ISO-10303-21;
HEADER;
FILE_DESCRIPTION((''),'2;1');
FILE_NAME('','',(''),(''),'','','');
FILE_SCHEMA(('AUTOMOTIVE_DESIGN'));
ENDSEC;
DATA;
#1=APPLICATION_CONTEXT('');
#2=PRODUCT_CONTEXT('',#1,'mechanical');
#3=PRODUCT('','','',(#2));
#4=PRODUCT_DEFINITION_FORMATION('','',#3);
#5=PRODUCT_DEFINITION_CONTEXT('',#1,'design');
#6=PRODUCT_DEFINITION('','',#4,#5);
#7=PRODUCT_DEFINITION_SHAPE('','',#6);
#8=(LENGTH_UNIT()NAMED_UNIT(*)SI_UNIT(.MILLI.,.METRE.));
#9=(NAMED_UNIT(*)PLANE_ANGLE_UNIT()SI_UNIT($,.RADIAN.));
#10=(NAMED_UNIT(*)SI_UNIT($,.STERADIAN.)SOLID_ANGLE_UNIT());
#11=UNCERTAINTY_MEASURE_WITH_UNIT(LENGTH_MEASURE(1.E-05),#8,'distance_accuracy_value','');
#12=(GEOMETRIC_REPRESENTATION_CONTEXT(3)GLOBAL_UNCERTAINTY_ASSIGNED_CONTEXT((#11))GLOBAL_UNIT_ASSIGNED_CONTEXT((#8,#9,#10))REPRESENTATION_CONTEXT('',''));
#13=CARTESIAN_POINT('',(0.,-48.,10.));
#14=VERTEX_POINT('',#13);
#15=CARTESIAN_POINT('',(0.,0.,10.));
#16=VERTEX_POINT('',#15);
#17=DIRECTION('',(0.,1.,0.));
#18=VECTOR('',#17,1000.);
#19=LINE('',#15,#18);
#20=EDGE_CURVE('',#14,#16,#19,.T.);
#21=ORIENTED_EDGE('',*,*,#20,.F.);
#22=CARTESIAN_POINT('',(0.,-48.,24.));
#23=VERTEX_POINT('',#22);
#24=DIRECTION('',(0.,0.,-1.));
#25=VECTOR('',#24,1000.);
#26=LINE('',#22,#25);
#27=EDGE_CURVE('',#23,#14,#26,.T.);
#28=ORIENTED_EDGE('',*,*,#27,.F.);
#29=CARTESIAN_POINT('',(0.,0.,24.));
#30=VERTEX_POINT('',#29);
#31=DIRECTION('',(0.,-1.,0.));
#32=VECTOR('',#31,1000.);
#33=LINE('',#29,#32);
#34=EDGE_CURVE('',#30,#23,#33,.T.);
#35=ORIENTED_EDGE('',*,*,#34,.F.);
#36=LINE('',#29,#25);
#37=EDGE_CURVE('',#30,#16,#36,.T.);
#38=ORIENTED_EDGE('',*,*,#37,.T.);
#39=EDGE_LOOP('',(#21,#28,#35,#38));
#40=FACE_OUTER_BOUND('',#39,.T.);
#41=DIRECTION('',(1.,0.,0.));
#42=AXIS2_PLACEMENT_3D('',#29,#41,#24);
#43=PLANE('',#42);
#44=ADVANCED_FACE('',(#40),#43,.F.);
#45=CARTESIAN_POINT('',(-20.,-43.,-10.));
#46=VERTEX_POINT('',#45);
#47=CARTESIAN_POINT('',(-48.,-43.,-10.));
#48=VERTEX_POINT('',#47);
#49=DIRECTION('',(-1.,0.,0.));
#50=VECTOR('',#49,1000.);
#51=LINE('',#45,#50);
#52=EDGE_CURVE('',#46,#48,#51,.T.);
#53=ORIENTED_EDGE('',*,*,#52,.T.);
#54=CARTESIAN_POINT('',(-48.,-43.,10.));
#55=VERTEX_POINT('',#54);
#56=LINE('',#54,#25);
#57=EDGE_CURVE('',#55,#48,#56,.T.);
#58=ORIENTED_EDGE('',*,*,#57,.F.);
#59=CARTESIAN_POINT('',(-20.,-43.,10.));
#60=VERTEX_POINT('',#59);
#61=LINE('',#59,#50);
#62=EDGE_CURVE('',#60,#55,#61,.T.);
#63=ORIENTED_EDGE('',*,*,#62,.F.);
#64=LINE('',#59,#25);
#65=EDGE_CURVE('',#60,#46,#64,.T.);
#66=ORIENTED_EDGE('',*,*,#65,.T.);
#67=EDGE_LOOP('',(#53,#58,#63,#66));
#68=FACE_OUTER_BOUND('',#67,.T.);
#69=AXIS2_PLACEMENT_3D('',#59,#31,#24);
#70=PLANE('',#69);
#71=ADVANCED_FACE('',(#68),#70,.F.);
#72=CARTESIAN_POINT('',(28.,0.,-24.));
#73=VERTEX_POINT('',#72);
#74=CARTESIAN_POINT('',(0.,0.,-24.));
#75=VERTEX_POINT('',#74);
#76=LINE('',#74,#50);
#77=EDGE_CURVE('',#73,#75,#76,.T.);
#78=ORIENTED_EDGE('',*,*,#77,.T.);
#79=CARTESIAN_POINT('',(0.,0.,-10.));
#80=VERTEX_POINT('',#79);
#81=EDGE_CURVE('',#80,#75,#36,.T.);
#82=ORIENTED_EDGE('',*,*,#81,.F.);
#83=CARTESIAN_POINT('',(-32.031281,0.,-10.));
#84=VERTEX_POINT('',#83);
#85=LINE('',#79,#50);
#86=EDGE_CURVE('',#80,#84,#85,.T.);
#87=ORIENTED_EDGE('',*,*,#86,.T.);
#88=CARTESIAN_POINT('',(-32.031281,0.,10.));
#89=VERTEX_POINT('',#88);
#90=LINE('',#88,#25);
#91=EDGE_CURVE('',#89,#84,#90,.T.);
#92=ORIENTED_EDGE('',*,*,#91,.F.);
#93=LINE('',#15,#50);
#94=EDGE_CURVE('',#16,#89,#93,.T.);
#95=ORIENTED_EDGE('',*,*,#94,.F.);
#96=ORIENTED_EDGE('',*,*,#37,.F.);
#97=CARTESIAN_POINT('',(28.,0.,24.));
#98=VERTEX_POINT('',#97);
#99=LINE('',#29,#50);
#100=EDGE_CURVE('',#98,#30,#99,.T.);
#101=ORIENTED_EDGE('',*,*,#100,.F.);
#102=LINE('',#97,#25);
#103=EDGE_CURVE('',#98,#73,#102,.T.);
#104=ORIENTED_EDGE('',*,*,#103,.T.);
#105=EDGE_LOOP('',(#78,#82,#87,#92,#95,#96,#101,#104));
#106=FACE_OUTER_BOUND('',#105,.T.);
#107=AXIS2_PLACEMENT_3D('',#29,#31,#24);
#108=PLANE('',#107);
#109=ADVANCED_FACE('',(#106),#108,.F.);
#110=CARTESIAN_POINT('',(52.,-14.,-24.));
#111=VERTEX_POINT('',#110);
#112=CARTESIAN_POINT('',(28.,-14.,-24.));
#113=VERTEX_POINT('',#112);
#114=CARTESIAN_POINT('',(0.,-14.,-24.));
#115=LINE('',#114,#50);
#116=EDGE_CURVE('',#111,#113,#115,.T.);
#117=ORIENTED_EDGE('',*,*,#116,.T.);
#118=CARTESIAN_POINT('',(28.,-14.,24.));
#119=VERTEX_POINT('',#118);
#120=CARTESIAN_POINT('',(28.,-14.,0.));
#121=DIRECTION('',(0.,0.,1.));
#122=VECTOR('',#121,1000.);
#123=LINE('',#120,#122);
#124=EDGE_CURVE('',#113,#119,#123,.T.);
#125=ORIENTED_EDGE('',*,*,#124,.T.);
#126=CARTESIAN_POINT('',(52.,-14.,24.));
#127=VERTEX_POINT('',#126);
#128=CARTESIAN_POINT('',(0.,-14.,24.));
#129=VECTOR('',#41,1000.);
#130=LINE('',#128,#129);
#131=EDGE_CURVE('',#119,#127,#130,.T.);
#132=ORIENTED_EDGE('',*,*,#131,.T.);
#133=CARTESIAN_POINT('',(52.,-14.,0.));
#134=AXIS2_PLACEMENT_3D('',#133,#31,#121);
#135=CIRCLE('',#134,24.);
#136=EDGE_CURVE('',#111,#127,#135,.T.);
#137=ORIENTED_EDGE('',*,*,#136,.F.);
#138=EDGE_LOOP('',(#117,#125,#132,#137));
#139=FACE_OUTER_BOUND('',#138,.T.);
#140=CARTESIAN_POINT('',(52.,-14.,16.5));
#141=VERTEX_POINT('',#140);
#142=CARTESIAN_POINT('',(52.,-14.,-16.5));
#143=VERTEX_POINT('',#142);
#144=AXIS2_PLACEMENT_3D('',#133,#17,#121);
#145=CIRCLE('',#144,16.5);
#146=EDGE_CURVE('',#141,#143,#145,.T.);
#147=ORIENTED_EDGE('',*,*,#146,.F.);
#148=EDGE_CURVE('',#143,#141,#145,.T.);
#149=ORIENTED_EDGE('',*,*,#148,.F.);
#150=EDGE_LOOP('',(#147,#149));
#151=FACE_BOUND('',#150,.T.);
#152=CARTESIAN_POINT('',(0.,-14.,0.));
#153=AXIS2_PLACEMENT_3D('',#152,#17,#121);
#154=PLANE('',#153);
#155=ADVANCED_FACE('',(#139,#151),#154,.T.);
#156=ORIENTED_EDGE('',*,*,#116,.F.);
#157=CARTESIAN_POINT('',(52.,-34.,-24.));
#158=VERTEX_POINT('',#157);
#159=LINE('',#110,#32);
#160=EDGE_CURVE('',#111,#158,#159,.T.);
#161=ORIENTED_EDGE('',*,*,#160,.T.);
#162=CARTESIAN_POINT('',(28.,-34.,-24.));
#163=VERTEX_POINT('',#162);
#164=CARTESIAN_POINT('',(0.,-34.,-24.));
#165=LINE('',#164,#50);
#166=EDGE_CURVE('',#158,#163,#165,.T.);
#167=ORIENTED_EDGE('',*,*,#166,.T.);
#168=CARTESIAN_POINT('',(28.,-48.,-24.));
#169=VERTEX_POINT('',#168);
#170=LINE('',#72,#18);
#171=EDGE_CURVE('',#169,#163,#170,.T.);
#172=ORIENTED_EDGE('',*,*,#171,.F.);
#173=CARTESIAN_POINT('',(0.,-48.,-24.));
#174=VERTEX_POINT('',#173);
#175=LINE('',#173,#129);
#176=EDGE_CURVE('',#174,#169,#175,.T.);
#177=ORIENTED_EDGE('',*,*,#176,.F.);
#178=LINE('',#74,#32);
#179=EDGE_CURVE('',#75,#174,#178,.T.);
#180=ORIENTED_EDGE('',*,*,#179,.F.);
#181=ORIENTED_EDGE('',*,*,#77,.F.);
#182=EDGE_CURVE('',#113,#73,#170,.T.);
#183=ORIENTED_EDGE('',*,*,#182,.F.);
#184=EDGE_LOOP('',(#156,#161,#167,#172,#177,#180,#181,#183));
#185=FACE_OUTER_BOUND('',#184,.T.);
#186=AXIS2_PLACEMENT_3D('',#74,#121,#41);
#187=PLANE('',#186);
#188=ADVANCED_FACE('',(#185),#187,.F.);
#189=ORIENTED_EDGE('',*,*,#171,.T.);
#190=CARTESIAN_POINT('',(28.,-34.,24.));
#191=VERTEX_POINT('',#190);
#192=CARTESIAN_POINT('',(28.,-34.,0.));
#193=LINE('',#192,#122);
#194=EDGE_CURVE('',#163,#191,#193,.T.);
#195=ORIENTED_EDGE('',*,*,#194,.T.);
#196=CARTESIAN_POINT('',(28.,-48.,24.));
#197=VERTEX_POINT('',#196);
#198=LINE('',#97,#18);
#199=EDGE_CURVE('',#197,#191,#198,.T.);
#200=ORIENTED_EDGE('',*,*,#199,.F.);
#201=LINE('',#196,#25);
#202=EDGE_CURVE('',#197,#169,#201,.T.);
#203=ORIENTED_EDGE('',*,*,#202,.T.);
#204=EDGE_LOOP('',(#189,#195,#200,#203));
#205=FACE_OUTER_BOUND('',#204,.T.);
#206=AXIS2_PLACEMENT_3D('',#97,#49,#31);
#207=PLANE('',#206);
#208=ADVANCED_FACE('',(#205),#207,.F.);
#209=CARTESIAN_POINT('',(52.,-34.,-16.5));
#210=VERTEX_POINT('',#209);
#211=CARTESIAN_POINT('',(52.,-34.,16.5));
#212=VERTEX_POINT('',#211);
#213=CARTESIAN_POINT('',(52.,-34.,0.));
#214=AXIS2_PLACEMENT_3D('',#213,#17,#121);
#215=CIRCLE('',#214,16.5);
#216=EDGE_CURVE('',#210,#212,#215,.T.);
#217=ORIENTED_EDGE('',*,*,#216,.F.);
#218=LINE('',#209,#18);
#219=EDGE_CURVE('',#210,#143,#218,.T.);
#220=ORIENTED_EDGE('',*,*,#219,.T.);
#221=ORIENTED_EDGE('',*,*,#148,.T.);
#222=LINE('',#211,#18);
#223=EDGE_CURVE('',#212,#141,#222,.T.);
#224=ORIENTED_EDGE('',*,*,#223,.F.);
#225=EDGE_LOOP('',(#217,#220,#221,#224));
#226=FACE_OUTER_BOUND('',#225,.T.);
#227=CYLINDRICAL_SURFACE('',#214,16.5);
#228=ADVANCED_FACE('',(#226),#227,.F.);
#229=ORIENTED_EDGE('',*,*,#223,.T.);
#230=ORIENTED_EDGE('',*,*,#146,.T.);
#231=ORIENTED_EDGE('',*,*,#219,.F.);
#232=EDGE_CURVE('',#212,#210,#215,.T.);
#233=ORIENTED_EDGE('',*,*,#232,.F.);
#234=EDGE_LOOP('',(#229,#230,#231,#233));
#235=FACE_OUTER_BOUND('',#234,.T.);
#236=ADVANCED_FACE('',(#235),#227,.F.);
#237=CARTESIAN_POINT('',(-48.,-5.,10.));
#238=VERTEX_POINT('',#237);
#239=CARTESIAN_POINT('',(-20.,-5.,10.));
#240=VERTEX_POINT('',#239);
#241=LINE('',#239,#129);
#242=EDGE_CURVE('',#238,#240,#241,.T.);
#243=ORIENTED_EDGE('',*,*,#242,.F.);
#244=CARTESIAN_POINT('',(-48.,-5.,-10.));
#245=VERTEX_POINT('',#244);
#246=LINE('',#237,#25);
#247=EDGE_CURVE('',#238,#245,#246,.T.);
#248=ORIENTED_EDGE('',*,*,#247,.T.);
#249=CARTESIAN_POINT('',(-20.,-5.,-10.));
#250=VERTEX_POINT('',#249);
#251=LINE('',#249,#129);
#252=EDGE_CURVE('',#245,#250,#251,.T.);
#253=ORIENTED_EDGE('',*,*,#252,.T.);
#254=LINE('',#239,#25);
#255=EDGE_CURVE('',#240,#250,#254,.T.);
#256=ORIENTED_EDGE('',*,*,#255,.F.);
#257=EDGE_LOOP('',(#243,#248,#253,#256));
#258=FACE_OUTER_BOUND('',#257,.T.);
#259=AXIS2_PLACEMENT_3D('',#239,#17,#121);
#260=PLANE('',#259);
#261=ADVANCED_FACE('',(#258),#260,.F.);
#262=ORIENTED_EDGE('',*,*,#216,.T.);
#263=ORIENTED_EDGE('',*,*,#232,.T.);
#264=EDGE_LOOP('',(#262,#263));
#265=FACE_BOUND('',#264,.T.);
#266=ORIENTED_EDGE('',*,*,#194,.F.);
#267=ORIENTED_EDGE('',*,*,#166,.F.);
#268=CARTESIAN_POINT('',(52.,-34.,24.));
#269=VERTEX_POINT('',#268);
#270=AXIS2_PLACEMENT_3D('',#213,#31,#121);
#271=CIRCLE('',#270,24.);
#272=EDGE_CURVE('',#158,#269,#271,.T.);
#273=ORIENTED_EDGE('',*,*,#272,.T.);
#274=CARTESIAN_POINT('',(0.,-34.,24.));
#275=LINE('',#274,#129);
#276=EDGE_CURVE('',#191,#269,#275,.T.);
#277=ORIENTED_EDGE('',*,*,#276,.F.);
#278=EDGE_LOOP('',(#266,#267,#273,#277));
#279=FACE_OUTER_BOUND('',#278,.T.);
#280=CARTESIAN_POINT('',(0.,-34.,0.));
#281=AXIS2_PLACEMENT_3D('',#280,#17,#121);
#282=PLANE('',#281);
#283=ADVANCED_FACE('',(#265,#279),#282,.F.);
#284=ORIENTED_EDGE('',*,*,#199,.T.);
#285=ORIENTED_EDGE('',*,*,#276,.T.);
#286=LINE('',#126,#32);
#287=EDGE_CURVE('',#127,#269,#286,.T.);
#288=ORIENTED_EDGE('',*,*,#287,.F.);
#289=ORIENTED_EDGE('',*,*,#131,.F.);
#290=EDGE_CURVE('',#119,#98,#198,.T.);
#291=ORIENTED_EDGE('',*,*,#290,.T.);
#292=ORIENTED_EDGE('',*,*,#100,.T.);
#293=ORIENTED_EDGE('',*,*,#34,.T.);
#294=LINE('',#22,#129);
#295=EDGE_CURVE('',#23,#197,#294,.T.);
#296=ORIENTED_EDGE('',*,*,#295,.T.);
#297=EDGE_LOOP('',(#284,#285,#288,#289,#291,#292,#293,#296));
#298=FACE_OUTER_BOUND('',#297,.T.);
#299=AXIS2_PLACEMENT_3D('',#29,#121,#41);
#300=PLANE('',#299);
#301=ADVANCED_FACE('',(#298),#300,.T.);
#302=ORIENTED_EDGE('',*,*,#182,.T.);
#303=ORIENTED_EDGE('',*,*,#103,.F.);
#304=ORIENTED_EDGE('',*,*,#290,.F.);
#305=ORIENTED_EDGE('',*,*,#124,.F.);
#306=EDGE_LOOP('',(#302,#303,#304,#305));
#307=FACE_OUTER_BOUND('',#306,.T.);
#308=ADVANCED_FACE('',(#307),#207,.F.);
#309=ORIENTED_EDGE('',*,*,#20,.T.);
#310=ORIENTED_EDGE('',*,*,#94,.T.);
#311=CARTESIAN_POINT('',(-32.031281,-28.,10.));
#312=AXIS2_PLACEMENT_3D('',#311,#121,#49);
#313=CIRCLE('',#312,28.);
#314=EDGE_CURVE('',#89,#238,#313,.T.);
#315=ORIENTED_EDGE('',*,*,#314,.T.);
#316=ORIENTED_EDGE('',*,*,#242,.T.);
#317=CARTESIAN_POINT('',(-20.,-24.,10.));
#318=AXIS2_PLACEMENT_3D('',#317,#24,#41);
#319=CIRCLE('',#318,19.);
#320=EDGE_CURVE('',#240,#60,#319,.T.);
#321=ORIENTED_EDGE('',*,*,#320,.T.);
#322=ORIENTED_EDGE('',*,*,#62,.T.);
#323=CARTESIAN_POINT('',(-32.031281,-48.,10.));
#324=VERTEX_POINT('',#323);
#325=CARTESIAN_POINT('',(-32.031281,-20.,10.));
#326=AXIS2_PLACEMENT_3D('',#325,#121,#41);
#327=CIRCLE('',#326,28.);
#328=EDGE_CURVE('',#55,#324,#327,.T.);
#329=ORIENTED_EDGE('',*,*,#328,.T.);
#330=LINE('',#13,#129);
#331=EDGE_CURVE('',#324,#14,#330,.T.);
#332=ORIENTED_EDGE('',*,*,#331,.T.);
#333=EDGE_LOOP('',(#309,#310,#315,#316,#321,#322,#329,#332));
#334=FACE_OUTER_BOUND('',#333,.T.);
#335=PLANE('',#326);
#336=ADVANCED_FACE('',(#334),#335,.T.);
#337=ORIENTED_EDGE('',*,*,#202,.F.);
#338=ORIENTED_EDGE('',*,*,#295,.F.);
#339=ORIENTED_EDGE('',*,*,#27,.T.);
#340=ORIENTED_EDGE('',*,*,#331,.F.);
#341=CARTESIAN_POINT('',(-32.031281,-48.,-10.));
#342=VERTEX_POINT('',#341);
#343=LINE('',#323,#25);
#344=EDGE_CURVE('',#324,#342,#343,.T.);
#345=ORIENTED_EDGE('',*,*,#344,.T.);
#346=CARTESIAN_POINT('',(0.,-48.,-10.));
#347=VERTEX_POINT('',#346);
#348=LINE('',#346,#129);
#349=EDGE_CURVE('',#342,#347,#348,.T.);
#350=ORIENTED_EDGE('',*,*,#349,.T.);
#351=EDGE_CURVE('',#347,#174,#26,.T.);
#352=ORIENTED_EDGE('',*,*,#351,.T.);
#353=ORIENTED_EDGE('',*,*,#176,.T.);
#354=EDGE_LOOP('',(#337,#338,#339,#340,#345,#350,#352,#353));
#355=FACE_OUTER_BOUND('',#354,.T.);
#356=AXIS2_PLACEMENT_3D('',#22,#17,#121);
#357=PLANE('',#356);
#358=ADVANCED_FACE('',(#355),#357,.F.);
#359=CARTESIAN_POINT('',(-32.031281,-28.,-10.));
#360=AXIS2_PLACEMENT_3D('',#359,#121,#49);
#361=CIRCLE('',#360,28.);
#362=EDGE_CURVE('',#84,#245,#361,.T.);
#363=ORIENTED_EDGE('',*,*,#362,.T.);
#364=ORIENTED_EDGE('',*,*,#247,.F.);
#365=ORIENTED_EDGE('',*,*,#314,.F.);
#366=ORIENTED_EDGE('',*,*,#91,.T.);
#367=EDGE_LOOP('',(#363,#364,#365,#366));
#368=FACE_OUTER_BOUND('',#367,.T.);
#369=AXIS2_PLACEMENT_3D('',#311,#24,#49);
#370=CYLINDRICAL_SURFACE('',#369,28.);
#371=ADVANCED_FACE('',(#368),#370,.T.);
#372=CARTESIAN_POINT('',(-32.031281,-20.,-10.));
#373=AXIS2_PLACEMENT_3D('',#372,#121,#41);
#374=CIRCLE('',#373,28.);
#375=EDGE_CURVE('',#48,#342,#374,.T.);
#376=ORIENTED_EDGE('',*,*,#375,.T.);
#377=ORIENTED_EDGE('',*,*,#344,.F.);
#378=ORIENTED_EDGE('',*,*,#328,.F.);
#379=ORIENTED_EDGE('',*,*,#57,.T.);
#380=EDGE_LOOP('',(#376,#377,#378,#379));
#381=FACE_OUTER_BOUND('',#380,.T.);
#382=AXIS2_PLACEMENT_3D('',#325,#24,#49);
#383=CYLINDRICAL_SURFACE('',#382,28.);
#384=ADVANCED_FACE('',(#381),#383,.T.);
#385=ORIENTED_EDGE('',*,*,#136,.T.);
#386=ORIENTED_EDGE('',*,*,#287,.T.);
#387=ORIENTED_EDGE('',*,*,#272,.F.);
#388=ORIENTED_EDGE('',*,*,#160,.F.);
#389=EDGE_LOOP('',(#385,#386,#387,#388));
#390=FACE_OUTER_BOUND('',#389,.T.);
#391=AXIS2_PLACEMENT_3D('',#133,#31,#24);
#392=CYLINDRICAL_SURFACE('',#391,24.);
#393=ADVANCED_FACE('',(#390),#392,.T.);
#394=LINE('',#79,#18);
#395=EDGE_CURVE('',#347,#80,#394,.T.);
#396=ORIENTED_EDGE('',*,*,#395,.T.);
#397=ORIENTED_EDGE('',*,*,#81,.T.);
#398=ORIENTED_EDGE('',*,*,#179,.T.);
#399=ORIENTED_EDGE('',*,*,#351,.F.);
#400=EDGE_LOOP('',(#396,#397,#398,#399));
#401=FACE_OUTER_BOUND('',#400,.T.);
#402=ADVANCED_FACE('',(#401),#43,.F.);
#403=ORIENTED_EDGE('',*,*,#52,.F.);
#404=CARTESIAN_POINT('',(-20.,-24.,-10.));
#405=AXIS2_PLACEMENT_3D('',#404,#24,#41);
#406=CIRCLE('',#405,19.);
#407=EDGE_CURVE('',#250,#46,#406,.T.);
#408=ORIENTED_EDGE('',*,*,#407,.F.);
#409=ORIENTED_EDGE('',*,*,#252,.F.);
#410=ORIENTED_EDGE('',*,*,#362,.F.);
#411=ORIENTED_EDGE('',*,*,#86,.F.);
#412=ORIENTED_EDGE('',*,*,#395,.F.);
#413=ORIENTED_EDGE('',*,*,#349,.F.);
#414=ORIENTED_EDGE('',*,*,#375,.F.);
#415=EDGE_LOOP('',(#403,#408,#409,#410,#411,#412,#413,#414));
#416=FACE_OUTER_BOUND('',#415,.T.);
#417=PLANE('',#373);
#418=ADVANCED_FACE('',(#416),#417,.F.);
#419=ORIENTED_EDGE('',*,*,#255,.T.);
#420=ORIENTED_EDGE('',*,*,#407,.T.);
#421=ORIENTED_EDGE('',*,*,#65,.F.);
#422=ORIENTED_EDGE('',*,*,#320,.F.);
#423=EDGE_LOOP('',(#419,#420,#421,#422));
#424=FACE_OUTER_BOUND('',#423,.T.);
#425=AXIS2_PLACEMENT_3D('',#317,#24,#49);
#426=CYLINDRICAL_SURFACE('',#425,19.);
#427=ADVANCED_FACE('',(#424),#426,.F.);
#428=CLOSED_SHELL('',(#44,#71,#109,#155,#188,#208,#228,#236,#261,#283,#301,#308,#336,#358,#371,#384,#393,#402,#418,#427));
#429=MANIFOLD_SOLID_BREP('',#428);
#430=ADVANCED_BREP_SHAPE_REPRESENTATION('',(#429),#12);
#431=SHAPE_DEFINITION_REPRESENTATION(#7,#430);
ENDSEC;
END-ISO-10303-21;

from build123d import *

# Parameters (mm, degrees)
BASE_BLOCK_SKETCH_W       = 28
BASE_BLOCK_SKETCH_H       = 48
BASE_BLOCK_DEPTH          = 24
FORK_ARMS_DEPTH           = 10
FORK_ARC_CUT_SKETCH_R33_R = 16.5
FORK_ARC_CUT_DEPTH        = 20
EYE_START                 = -24
EYE_LUG_WITH_BORE_DEPTH   = 10


with BuildPart() as part:
    # Base Block Sketch → Base Block (new, symmetric)
    with BuildSketch(Plane.XY):
        with Locations((14, -24)):
            Rectangle(BASE_BLOCK_SKETCH_W, BASE_BLOCK_SKETCH_H)
    extrude(amount=BASE_BLOCK_DEPTH, both=True)

    # Fork Arms Sketch → Fork Arms (add, symmetric)
    with BuildSketch(Plane(origin=(0, -24, 0), x_dir=(1, 0, 0), z_dir=(0, 1, 0))):
        with BuildLine():
            Line((52, 24), (28, 24))
            Line((28, 24), (28, -24))
            Line((28, -24), (52, -24))
            ThreePointArc((52, -24), (76, 0), (52, 24))
        make_face()
    extrude(amount=FORK_ARMS_DEPTH, both=True)

    # Fork Arc Cut Sketch R33 → Fork Arc Cut (cut)
    with BuildSketch(Plane(origin=(0, -14, 0), x_dir=(1, 0, 0), z_dir=(0, 1, 0))):
        with Locations(Location((52, 0, 0), (0, 0, 270))):
            Circle(FORK_ARC_CUT_SKETCH_R33_R)
    extrude(amount=-FORK_ARC_CUT_DEPTH, mode=Mode.SUBTRACT)

    # Eye Lug Sketch → Eye Lug With Bore (add, symmetric)
    with BuildSketch(Plane.XY.offset(24).offset(EYE_START)):
        with BuildLine():
            Line((0, 0), (-32.031280577, 0))
            ThreePointArc((-32.031280577, 0), (-40.397880843, -1.279221568), (-48, -5))
            Line((-48, -5), (-20, -5))
            ThreePointArc((-20, -5), (-1, -24), (-20, -43))
            Line((-20, -43), (-48, -43))
            ThreePointArc((-48, -43), (-40.397880843, -46.720778432), (-32.031280577, -48))
            Line((-32.031280577, -48), (0, -48))
            Line((0, -48), (0, 0))
        make_face()
    extrude(amount=EYE_LUG_WITH_BORE_DEPTH, both=True)


solid = part.part
